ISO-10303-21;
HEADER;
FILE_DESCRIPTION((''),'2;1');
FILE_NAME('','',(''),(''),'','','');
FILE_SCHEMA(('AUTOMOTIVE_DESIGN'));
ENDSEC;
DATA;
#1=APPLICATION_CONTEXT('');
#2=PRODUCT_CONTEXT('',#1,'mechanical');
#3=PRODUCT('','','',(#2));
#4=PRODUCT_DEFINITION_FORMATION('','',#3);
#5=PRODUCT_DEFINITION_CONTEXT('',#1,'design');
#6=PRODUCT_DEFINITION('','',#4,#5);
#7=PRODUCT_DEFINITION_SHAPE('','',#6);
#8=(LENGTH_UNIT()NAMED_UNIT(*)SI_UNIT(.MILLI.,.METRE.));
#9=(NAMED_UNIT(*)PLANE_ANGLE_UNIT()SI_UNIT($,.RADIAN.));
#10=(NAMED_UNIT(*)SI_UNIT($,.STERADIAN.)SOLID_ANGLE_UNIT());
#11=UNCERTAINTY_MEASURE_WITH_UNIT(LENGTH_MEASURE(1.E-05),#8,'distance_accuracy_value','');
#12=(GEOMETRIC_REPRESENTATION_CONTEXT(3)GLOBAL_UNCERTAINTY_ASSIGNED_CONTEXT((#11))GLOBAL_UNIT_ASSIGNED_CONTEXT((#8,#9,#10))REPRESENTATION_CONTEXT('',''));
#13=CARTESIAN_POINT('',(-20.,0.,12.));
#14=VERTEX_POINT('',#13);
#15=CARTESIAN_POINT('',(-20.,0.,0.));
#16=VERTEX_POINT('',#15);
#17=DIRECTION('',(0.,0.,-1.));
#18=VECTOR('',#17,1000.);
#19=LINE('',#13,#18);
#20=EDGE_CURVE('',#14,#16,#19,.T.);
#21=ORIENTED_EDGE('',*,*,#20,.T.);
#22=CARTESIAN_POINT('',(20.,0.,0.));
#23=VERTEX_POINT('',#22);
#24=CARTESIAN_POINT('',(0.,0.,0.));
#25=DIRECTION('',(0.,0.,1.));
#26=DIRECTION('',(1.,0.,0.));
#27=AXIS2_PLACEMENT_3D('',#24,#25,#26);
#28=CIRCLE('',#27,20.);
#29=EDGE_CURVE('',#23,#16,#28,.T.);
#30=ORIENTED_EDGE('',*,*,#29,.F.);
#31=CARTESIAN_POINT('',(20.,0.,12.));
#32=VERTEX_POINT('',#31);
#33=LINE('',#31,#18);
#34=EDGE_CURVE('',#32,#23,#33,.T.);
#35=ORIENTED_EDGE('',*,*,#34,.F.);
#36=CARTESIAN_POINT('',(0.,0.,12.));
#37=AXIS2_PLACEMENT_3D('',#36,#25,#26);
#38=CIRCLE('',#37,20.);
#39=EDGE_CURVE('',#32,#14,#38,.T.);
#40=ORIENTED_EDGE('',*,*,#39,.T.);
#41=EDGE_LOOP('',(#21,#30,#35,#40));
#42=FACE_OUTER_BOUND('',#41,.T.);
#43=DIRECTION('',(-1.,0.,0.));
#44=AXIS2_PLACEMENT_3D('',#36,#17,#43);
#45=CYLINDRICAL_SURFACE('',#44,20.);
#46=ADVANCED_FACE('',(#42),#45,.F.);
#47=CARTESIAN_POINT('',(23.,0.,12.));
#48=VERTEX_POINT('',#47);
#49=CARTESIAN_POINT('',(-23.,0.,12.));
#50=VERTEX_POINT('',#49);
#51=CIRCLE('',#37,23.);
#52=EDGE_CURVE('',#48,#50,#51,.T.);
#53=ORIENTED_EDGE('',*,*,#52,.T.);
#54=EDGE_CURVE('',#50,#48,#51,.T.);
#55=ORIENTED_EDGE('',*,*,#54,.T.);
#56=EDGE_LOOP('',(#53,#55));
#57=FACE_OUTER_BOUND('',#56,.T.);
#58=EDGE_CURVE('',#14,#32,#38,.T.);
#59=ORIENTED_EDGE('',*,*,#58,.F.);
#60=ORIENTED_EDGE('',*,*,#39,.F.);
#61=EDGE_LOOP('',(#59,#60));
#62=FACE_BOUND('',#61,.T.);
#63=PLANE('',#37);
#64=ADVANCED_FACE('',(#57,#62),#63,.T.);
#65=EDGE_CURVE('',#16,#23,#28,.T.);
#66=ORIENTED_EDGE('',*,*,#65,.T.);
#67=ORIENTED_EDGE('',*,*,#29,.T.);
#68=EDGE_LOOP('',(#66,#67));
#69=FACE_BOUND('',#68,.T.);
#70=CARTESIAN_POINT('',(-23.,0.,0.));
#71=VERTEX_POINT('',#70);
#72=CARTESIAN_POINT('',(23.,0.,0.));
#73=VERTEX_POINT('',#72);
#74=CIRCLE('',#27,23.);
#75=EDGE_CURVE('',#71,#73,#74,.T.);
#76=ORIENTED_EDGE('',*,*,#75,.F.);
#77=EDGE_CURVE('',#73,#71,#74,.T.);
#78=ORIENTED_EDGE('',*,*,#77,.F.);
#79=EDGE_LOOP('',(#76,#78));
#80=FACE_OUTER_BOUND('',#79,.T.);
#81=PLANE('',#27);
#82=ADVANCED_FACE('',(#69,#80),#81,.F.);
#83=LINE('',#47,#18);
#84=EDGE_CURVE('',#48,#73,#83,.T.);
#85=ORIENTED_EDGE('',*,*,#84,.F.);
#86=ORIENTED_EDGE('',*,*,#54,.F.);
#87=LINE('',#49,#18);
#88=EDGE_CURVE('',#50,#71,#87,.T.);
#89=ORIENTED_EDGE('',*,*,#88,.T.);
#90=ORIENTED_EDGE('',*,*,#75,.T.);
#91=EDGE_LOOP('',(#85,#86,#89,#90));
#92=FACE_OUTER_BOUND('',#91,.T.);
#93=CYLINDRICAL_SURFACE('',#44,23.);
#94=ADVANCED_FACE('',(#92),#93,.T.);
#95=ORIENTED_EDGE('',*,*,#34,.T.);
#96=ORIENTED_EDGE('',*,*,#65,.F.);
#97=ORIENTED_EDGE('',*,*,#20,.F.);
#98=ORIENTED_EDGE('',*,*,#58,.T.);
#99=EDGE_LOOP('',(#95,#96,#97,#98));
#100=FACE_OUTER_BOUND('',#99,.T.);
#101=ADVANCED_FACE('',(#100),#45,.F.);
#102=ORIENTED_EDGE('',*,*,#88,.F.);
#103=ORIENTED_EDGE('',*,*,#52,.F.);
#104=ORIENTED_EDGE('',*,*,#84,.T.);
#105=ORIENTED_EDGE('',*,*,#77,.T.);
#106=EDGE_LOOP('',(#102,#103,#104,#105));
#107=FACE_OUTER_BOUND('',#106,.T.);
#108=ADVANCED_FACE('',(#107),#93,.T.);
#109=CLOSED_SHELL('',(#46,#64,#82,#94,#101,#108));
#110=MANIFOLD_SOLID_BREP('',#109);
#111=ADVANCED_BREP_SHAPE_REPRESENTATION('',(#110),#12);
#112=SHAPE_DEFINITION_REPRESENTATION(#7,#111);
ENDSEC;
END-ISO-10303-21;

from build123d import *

# Parameters (mm, degrees)
SKETCH_1_R      = 23
SKETCH_1_R_2    = 20
EXTRUDE_1_DEPTH = 12


with BuildPart() as part:
    # 草图1 → 凸台-拉伸1 (new body)
    with BuildSketch(Plane.XY):
        Circle(SKETCH_1_R)
        Circle(SKETCH_1_R_2, mode=Mode.SUBTRACT)
    extrude(amount=EXTRUDE_1_DEPTH)


solid = part.part
